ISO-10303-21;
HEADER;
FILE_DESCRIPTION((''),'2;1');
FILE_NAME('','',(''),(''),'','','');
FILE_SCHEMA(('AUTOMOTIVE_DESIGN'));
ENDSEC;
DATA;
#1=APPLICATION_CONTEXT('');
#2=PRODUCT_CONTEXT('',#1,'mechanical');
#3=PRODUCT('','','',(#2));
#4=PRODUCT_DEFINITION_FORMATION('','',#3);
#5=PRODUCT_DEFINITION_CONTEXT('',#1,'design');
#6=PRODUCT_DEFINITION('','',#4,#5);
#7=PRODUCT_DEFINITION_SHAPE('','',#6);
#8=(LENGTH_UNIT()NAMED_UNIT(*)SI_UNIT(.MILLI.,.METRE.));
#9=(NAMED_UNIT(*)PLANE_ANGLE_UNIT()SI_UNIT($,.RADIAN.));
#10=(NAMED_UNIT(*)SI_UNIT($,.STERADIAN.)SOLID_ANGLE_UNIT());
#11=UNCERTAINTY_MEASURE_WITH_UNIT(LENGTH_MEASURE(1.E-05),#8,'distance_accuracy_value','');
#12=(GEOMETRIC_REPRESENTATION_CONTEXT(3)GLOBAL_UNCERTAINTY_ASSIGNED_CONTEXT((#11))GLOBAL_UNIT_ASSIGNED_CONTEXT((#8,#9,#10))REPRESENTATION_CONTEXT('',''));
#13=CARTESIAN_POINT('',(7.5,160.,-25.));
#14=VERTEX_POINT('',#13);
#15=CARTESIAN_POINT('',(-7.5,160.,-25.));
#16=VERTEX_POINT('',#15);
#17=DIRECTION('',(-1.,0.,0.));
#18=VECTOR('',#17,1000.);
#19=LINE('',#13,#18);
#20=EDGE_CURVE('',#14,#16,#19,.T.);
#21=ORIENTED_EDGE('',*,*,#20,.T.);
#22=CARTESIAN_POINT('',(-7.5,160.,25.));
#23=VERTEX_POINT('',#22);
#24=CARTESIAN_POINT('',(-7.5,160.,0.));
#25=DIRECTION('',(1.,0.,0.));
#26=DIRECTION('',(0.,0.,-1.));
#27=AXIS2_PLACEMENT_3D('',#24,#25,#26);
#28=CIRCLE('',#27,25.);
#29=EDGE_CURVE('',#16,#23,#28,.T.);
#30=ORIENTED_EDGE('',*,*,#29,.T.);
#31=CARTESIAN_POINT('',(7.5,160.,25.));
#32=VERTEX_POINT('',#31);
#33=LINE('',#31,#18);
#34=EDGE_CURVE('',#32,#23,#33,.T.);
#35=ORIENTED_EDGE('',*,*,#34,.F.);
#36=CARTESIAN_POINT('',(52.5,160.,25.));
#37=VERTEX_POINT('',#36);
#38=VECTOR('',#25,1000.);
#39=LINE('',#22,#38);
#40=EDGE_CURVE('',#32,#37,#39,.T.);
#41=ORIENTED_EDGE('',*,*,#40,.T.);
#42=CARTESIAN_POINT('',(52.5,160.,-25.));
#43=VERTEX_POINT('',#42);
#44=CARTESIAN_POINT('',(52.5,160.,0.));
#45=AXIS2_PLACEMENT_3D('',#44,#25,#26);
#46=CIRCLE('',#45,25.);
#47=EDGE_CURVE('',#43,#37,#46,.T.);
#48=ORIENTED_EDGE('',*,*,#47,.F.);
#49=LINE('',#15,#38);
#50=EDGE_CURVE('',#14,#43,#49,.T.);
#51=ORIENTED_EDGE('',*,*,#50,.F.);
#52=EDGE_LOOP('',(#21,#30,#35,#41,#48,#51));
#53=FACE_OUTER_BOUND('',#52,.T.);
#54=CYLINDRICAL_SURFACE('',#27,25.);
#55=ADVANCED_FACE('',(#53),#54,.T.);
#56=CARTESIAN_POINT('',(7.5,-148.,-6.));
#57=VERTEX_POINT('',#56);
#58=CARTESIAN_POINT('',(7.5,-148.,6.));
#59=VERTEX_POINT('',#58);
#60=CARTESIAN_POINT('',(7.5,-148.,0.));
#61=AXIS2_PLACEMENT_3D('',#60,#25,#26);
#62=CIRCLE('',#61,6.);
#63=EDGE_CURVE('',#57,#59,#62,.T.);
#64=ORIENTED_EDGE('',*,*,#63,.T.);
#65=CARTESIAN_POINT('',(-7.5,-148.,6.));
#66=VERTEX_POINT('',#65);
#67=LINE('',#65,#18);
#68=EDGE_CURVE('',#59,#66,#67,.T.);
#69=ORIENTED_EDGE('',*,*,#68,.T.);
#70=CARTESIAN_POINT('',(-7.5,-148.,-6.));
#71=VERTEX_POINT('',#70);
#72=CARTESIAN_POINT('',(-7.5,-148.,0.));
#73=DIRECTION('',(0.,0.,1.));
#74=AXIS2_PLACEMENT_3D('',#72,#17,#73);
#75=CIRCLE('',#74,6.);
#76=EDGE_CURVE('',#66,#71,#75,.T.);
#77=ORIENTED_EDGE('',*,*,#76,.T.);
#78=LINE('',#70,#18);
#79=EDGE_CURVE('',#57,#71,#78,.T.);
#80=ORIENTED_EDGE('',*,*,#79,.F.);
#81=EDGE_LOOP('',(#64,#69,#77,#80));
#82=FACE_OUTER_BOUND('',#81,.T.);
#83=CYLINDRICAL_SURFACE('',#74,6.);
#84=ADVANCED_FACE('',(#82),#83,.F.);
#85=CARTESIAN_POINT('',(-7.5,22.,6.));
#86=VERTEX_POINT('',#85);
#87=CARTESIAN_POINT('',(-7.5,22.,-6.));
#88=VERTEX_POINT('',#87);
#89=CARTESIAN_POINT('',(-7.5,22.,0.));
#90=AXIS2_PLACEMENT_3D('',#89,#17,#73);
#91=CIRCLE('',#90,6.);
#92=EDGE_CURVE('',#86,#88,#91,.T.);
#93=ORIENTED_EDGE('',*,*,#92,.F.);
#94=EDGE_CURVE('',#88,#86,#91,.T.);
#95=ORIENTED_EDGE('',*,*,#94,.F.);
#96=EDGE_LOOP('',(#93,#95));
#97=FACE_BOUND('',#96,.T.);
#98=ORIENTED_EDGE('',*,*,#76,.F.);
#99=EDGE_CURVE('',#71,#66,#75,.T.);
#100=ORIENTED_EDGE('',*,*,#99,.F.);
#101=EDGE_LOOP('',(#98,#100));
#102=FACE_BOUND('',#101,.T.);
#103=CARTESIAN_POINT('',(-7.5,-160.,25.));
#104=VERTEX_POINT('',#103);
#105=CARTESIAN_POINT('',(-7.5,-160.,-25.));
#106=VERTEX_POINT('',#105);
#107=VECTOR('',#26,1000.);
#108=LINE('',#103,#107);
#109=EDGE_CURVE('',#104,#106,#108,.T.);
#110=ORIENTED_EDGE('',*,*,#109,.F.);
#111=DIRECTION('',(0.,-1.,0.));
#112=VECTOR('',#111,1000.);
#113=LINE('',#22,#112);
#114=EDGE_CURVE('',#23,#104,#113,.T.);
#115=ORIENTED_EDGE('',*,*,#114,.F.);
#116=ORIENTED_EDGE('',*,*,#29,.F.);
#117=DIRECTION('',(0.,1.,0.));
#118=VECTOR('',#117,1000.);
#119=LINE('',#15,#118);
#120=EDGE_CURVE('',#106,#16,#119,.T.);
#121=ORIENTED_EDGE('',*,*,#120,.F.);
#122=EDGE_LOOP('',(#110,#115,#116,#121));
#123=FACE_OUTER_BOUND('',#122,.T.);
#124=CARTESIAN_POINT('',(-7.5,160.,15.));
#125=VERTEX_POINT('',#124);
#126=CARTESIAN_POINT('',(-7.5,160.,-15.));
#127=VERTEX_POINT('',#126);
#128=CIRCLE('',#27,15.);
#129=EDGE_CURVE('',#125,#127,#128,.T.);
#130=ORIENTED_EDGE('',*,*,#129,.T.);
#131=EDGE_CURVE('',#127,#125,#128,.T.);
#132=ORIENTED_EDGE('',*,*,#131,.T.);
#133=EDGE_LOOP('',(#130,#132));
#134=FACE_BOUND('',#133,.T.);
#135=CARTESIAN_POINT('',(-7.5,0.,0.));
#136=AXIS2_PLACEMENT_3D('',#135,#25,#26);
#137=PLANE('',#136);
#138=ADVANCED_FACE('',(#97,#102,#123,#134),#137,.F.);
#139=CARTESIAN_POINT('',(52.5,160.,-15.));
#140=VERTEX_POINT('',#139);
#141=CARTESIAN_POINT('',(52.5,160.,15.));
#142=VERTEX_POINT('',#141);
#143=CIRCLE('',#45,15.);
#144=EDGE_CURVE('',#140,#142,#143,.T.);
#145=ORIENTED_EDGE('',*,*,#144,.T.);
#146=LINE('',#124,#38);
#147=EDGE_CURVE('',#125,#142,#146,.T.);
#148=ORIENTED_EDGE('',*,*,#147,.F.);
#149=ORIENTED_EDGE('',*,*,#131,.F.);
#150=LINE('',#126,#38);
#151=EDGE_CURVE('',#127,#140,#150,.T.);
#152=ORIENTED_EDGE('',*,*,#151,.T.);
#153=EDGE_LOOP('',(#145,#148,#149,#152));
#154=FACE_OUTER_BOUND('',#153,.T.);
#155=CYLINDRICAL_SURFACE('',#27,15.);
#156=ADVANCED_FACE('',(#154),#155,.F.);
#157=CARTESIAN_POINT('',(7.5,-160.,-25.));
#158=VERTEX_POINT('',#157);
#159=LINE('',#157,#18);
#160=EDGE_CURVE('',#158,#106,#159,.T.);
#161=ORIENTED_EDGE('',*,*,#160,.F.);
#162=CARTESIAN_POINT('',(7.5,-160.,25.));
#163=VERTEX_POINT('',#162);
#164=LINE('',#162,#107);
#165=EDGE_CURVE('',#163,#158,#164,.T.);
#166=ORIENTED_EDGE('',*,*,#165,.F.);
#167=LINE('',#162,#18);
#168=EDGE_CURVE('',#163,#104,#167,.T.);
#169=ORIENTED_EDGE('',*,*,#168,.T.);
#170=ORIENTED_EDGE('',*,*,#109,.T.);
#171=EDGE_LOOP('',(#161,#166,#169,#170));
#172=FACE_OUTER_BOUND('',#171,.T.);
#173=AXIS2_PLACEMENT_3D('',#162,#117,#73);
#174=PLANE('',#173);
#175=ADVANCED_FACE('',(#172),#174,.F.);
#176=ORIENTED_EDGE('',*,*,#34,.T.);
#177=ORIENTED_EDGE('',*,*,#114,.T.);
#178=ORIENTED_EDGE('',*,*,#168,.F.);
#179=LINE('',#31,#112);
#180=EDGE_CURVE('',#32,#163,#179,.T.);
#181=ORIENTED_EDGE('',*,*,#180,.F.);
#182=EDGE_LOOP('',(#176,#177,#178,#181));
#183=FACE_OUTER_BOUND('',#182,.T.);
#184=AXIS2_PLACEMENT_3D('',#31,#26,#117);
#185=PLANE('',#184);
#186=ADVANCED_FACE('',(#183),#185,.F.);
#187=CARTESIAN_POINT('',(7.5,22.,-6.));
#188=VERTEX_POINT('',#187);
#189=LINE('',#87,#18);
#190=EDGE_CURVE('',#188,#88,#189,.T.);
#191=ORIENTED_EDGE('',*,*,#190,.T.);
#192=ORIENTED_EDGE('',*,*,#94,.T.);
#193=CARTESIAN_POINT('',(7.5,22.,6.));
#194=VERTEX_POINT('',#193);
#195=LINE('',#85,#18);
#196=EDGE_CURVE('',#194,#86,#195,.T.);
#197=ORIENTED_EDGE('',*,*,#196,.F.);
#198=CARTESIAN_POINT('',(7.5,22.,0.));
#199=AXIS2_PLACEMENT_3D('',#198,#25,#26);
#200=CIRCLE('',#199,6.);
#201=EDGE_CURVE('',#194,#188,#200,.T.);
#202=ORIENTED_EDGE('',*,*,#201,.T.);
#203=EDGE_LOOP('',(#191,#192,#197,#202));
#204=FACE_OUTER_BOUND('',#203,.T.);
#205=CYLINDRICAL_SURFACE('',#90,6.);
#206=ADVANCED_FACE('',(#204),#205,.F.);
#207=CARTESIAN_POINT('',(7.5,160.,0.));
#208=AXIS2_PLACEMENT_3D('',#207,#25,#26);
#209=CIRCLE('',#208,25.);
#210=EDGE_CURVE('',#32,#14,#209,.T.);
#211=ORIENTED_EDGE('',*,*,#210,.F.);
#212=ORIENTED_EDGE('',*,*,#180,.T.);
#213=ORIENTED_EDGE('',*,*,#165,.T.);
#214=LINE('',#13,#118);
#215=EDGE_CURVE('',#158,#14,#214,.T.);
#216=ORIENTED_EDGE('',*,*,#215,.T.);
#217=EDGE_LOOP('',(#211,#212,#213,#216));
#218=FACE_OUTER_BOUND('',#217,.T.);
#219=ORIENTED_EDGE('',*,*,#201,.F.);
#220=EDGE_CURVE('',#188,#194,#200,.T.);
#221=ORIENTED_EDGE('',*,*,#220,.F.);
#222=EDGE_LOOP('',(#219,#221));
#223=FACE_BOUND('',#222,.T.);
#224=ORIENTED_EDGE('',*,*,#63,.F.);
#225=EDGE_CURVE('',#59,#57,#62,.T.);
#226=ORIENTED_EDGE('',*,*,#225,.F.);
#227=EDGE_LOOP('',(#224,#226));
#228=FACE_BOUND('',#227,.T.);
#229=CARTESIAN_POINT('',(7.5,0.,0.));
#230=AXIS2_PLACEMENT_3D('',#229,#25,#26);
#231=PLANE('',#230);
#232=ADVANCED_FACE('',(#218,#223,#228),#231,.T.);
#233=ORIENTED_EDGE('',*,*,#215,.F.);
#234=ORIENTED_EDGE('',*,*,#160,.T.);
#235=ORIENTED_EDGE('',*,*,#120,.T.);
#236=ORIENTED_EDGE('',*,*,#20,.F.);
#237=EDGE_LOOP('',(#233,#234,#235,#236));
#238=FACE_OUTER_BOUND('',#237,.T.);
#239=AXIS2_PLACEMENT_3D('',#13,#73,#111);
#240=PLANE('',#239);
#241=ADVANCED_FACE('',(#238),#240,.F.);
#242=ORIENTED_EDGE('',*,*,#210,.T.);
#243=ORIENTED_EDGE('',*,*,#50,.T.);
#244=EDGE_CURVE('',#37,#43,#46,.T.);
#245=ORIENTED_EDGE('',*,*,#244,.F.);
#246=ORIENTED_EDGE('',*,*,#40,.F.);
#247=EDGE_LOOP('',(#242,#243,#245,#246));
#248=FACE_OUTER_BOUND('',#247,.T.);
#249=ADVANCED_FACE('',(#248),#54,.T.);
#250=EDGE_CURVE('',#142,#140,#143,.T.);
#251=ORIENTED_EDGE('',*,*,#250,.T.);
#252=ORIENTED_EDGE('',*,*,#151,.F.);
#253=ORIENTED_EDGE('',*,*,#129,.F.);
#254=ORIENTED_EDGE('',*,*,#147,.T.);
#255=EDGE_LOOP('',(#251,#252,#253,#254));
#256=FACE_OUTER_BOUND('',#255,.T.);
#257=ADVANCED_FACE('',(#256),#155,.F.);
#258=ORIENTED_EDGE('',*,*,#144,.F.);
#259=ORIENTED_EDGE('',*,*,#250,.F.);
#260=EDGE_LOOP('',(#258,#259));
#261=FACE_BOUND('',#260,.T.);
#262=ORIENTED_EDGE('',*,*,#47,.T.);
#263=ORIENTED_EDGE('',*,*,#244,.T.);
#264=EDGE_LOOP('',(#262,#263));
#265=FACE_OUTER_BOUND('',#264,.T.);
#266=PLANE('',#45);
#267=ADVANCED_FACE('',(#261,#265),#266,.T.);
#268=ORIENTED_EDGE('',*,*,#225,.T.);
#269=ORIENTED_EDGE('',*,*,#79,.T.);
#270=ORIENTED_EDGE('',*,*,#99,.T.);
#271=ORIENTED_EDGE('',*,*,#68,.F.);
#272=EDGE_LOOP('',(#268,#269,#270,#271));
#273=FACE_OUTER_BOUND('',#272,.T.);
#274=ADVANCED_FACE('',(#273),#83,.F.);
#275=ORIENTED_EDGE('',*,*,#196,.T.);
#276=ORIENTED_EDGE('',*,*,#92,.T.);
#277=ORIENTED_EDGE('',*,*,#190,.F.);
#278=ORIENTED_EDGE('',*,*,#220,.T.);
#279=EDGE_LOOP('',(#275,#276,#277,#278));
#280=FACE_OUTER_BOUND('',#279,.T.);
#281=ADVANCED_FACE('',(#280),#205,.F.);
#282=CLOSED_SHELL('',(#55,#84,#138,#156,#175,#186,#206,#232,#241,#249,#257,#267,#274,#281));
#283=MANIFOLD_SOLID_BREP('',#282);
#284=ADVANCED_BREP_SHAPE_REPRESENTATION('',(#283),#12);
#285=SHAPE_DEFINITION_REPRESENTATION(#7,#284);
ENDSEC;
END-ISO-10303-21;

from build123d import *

# Parameters (mm, degrees)
SKETCH_1_W              = 50
SKETCH_1_H              = 320
EXTRUDE_1_DEPTH         = 7.5
EXTRUDE_2_DEPTH         = 52.5
EXTRUDE_2_DEPTH_BACK    = 7.5
SKETCH_2_R              = 25
SKETCH_3_R              = 15
CUT_EXTRUDE_1_DEPTH     = 197.086715511
HOLE_WIZARD_12_0_12_1_D = 12


with BuildPart() as part:
    # 草图1 → 凸台-拉伸1 (new, symmetric)
    with BuildSketch(Plane(origin=(0, 0, 0), x_dir=(0, 0, -1), z_dir=(1, 0, 0))):
        Rectangle(SKETCH_1_W, SKETCH_1_H)
    extrude(amount=EXTRUDE_1_DEPTH, both=True)

    # 草图2 → 凸台-拉伸2 (add, two sides: drawn at the far end of the back side and taken through both)
    with BuildSketch(Plane(origin=(0, 0, 0), x_dir=(0, 0, -1), z_dir=(1, 0, 0)).offset(-EXTRUDE_2_DEPTH_BACK)):
        with Locations((0, 160)):
            Circle(SKETCH_2_R)
    extrude(amount=EXTRUDE_2_DEPTH + EXTRUDE_2_DEPTH_BACK)

    # 草图3 → 切除-拉伸1 (cut, through all)
    with BuildSketch(Plane(origin=(52.5, 0, 0), x_dir=(0, 0, -1), z_dir=(1, 0, 0))):
        with Locations((0, 160)):
            Circle(SKETCH_3_R)
    extrude(amount=-CUT_EXTRUDE_1_DEPTH, mode=Mode.SUBTRACT)

    # Ø12.0 (12) 直径孔1 (through all)
    with Locations(Plane.ZY.offset(7.5)):
        with Locations((0, 22), (0, -148)):
            Hole(HOLE_WIZARD_12_0_12_1_D / 2)


solid = part.part
